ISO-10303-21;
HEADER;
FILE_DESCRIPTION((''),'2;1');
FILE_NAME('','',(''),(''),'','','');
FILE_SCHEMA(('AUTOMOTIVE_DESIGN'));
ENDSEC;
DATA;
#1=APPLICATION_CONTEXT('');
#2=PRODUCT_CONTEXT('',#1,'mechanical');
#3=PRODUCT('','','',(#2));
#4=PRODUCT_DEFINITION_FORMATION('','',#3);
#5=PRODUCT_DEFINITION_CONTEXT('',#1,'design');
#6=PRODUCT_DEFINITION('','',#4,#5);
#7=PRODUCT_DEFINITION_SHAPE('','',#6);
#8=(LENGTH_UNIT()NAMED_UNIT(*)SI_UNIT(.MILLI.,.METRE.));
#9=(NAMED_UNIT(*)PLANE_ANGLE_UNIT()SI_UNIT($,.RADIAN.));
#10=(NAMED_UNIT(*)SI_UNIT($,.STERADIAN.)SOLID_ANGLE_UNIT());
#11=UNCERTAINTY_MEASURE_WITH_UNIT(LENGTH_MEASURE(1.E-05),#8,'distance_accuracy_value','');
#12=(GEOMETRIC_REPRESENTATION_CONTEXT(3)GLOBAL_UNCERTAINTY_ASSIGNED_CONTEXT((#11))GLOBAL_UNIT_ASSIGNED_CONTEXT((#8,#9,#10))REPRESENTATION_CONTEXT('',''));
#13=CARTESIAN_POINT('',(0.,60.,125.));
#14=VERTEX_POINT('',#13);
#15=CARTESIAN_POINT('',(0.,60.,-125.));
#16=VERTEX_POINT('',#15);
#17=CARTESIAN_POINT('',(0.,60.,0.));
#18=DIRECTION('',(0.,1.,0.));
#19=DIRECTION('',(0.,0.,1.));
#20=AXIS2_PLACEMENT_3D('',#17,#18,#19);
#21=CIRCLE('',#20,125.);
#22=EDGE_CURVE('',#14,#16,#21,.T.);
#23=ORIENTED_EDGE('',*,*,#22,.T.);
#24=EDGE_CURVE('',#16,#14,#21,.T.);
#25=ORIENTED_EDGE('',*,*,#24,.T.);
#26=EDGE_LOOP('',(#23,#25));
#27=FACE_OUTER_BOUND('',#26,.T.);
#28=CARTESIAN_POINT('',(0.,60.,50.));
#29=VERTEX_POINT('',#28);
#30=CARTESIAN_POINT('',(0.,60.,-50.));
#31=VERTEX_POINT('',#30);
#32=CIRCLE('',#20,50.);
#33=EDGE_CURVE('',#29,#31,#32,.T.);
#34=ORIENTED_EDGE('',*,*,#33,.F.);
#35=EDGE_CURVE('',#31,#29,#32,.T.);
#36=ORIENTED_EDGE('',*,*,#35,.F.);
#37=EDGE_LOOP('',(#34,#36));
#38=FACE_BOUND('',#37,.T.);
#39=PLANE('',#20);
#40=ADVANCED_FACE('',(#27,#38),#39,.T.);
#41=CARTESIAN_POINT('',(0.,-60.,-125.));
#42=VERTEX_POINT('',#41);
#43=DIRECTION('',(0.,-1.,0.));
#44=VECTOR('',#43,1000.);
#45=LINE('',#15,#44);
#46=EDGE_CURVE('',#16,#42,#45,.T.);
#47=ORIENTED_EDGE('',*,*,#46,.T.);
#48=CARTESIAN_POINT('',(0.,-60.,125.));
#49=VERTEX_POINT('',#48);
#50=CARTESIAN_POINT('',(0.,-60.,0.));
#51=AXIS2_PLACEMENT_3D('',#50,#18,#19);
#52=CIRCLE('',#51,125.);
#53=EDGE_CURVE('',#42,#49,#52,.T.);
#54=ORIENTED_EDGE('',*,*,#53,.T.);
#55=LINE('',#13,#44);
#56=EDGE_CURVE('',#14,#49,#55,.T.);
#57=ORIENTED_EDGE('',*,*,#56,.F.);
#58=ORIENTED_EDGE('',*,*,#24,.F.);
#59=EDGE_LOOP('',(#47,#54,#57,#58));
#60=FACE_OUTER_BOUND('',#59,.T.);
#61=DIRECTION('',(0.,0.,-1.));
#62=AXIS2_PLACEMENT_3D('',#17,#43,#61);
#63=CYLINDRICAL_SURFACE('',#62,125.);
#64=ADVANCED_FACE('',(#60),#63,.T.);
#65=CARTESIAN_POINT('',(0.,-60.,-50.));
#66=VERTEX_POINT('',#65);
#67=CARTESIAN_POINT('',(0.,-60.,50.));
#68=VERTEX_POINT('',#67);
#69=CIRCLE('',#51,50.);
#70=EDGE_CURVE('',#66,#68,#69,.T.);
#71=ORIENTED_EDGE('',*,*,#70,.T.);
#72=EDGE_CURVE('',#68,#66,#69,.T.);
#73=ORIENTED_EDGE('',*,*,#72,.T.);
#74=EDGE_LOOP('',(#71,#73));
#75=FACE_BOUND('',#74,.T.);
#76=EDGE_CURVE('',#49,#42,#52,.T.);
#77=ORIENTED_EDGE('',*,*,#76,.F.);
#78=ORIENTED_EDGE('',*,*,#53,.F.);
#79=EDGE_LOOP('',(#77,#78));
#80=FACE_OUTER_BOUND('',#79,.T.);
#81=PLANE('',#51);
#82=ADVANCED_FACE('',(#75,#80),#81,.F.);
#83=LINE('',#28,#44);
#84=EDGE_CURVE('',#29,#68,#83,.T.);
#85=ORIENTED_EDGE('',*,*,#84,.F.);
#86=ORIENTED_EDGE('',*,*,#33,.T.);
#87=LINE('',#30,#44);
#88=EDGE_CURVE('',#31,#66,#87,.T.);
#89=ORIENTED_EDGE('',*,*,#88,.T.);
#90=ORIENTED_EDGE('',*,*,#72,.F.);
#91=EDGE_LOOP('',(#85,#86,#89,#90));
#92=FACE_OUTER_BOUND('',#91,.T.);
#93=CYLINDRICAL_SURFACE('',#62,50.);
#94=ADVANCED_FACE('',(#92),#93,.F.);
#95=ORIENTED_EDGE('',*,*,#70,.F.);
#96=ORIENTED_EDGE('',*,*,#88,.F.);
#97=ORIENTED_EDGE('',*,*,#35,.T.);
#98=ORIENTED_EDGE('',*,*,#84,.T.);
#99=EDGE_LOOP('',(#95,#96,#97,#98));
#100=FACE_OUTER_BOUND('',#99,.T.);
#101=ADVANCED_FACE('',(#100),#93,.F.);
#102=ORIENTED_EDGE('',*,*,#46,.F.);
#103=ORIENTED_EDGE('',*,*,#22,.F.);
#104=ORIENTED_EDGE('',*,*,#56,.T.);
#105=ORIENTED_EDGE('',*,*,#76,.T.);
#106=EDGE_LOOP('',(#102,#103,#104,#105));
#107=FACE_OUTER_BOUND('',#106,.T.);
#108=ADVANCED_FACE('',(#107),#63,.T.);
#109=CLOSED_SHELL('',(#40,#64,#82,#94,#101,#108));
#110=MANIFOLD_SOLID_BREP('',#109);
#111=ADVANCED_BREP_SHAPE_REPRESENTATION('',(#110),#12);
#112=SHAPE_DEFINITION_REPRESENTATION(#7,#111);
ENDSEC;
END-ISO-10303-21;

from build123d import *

# Parameters (mm, degrees)
SKETCH1_R           = 125
SKETCH1_R_2         = 50
BOSS_EXTRUDE1_DEPTH = 60


with BuildPart() as part:
    # Sketch1 → Boss-Extrude1 (new, symmetric)
    with BuildSketch(Plane(origin=(0, 0, 0), x_dir=(1, 0, 0), z_dir=(0, 1, 0))):
        with Locations(Location((0, 0, 0), (0, 0, 270))):
            Circle(SKETCH1_R)
        with Locations(Location((0, 0, 0), (0, 0, 270))):
            Circle(SKETCH1_R_2, mode=Mode.SUBTRACT)
    extrude(amount=BOSS_EXTRUDE1_DEPTH, both=True)


solid = part.part
